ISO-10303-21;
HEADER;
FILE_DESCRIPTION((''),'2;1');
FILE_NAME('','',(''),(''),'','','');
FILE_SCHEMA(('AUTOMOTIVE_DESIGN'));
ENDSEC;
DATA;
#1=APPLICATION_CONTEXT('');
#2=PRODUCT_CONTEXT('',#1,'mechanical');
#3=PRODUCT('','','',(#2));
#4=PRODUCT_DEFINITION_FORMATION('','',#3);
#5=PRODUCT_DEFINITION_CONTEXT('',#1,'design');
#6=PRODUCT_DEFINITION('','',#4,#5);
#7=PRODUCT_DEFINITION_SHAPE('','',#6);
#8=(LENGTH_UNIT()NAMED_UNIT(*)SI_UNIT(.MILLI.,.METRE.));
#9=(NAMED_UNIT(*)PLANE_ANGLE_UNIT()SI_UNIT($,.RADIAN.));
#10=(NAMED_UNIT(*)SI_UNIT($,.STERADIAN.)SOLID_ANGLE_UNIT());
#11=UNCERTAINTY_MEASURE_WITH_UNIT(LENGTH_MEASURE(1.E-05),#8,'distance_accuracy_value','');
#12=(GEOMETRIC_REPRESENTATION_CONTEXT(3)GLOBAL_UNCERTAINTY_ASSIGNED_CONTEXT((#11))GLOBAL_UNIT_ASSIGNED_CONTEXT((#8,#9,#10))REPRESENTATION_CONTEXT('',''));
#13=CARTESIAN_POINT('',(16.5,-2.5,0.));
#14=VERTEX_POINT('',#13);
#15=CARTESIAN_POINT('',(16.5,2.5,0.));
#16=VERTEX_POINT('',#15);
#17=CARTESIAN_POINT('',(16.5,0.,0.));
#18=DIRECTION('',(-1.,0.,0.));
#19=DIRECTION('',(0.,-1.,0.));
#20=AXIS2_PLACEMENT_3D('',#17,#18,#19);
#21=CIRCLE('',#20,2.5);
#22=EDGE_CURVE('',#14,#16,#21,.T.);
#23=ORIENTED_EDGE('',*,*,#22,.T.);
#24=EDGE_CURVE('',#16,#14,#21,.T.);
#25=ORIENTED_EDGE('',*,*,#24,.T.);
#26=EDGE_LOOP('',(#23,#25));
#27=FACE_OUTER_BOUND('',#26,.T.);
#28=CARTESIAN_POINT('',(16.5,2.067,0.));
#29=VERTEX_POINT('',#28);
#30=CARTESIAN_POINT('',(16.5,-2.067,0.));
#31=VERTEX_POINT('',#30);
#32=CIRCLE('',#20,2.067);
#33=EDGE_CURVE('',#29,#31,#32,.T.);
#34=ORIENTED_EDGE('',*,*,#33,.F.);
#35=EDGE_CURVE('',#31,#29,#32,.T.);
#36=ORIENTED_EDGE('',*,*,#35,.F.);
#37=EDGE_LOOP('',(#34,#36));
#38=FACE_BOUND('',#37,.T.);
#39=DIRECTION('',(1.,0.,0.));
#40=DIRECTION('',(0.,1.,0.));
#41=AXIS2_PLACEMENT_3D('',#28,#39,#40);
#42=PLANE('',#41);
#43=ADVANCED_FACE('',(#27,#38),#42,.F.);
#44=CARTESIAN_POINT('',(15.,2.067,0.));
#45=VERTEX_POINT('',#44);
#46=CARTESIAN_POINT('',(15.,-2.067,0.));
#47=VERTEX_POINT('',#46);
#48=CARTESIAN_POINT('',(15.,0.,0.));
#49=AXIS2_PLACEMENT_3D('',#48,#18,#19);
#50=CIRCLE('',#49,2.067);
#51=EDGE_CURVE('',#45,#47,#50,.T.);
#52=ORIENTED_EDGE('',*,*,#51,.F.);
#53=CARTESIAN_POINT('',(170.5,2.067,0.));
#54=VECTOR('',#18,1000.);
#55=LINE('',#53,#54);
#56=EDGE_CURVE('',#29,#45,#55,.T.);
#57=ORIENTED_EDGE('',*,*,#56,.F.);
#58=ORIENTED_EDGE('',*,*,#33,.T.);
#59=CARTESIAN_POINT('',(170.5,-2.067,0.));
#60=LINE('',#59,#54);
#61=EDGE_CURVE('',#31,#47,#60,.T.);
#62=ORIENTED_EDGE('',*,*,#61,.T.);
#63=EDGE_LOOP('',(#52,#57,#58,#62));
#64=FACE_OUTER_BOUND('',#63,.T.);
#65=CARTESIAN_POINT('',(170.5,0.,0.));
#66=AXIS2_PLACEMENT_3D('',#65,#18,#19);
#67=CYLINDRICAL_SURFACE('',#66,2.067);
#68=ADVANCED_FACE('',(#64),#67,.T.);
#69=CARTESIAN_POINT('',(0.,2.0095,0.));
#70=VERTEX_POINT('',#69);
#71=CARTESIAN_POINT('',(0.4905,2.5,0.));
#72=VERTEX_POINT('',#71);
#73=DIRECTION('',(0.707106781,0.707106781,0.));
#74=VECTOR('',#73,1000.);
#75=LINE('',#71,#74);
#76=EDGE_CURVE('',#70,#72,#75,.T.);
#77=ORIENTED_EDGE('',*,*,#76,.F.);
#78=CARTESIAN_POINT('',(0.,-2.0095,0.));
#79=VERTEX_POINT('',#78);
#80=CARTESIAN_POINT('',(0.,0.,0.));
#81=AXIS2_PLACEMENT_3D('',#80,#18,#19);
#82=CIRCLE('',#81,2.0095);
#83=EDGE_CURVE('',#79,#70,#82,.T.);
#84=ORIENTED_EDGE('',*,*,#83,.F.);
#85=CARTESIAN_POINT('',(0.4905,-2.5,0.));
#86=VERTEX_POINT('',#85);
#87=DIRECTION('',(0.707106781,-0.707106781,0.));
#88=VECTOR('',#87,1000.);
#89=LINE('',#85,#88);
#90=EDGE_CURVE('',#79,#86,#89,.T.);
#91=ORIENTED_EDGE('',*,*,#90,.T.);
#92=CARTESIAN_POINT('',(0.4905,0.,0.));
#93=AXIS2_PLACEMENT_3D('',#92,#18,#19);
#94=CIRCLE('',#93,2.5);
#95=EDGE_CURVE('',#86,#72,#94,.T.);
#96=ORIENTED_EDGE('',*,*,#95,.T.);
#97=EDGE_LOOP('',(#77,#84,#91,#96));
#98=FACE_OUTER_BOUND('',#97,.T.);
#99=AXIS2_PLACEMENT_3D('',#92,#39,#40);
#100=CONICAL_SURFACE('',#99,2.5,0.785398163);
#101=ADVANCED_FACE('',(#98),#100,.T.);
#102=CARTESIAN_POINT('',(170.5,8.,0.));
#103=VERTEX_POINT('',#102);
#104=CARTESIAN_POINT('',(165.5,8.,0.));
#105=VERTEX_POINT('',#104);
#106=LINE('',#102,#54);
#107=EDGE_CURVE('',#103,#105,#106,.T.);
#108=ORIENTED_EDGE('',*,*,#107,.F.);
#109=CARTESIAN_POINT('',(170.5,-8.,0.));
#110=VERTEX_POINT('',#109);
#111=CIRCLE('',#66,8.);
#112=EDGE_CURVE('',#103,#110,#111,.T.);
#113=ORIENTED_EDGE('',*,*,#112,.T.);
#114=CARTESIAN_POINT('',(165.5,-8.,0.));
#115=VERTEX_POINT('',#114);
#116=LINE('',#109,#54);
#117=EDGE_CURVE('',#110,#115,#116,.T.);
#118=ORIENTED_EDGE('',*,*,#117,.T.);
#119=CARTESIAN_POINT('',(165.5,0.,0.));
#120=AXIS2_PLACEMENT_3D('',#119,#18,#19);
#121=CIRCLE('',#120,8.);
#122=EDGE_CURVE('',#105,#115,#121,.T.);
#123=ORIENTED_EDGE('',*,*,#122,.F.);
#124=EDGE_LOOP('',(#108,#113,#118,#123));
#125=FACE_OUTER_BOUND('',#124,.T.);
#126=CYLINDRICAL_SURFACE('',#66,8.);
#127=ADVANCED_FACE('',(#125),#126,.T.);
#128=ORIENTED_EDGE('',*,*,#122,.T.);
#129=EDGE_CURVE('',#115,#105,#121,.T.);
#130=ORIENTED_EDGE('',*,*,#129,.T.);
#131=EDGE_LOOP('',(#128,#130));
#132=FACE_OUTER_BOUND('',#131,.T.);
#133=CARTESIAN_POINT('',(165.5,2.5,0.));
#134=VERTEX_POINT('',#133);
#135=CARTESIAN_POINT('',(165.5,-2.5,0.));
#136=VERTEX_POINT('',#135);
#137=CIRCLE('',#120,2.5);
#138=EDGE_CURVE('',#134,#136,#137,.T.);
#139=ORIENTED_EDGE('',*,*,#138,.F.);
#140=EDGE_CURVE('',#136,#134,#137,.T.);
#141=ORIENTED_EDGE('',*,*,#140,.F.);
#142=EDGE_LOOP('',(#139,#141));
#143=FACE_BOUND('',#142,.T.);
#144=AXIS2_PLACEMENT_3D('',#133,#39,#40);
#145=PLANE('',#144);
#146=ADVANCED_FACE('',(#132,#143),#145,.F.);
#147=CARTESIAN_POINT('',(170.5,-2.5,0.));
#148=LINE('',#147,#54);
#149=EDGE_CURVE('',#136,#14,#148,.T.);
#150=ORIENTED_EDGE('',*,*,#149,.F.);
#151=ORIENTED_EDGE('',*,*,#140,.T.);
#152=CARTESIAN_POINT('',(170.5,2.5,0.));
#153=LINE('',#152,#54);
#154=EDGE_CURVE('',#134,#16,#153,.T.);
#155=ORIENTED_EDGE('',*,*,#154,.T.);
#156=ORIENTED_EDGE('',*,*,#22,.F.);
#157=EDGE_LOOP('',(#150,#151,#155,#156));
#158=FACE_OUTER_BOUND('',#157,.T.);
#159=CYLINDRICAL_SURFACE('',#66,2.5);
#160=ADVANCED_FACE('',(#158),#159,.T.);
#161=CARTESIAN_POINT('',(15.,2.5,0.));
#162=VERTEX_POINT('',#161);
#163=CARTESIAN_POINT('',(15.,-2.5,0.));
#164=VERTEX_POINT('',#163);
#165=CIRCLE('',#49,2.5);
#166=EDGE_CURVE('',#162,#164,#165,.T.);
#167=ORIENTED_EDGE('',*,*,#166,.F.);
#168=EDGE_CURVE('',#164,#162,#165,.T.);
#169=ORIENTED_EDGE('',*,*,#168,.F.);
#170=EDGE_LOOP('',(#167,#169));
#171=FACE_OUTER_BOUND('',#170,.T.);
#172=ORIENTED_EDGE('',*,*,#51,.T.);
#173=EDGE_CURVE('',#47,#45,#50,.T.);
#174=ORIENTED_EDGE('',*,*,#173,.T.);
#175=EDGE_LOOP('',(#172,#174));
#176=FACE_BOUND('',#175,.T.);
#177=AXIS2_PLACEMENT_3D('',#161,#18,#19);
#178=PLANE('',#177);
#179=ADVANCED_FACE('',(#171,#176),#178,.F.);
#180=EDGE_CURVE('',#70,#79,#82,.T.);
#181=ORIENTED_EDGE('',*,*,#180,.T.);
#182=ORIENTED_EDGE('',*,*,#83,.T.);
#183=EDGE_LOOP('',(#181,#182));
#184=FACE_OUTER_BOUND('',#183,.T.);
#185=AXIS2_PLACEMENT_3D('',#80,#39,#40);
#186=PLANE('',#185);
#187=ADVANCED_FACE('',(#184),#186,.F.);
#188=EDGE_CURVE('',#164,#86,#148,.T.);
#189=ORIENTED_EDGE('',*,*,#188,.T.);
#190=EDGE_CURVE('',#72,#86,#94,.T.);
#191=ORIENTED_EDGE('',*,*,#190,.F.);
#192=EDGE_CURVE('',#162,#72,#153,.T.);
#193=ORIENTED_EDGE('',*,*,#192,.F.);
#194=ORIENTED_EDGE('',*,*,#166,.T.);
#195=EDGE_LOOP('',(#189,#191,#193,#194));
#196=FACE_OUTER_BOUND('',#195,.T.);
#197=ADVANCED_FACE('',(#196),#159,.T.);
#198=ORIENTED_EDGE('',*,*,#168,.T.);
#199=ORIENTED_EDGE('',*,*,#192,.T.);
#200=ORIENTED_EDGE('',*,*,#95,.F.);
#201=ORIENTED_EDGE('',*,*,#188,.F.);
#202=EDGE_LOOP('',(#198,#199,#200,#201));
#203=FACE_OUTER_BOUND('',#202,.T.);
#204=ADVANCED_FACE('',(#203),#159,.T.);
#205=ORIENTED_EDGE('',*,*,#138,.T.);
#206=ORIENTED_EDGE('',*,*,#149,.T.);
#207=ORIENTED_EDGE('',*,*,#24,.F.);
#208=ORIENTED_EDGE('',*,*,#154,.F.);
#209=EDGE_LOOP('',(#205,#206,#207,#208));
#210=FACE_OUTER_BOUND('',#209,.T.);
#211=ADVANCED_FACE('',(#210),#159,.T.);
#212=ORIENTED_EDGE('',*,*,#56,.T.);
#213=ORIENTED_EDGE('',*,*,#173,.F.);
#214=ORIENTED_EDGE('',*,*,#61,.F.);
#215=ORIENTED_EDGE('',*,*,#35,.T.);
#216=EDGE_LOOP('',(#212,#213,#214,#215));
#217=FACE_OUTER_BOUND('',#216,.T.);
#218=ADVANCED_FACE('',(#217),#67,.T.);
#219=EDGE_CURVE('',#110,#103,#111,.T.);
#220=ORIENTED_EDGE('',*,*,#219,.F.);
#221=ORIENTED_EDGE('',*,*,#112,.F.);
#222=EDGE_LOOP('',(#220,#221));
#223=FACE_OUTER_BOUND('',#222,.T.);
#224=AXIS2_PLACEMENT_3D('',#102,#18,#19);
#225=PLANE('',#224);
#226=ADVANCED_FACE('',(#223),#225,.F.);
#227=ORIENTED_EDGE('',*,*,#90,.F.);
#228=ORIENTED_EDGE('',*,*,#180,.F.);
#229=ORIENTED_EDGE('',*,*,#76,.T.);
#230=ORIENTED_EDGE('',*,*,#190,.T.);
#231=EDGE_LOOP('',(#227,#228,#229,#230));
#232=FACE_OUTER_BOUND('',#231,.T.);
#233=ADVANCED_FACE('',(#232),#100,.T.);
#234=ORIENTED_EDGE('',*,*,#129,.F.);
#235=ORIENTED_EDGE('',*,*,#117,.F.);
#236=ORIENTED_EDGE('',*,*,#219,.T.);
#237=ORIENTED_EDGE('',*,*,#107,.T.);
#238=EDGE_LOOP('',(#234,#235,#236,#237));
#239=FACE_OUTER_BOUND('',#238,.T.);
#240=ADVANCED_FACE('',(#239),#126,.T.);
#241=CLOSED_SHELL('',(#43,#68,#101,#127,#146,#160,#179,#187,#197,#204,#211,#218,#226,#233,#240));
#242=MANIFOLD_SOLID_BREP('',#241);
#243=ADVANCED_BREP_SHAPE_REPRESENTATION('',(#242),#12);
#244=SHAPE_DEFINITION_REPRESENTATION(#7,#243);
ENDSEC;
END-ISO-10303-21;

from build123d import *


with BuildPart() as part:
    # Sketch1 → Revolve1 (revolve)
    with BuildSketch(Plane.XY, mode=Mode.PRIVATE) as revolve1_sk:
        Polygon((0, 0), (0, 2.0095), (0.4905, 2.5), (15, 2.5), (15, 2.067), (16.5, 2.067), (16.5, 2.5), (165.5, 2.5), (165.5, 8), (170.5, 8), (170.5, 0), align=None)
    revolve(revolve1_sk.sketch.rotate(Axis((170.5, 0, 0), (-1, 0, 0)), 180), axis=Axis((170.5, 0, 0), (-1, 0, 0)))


solid = part.part
